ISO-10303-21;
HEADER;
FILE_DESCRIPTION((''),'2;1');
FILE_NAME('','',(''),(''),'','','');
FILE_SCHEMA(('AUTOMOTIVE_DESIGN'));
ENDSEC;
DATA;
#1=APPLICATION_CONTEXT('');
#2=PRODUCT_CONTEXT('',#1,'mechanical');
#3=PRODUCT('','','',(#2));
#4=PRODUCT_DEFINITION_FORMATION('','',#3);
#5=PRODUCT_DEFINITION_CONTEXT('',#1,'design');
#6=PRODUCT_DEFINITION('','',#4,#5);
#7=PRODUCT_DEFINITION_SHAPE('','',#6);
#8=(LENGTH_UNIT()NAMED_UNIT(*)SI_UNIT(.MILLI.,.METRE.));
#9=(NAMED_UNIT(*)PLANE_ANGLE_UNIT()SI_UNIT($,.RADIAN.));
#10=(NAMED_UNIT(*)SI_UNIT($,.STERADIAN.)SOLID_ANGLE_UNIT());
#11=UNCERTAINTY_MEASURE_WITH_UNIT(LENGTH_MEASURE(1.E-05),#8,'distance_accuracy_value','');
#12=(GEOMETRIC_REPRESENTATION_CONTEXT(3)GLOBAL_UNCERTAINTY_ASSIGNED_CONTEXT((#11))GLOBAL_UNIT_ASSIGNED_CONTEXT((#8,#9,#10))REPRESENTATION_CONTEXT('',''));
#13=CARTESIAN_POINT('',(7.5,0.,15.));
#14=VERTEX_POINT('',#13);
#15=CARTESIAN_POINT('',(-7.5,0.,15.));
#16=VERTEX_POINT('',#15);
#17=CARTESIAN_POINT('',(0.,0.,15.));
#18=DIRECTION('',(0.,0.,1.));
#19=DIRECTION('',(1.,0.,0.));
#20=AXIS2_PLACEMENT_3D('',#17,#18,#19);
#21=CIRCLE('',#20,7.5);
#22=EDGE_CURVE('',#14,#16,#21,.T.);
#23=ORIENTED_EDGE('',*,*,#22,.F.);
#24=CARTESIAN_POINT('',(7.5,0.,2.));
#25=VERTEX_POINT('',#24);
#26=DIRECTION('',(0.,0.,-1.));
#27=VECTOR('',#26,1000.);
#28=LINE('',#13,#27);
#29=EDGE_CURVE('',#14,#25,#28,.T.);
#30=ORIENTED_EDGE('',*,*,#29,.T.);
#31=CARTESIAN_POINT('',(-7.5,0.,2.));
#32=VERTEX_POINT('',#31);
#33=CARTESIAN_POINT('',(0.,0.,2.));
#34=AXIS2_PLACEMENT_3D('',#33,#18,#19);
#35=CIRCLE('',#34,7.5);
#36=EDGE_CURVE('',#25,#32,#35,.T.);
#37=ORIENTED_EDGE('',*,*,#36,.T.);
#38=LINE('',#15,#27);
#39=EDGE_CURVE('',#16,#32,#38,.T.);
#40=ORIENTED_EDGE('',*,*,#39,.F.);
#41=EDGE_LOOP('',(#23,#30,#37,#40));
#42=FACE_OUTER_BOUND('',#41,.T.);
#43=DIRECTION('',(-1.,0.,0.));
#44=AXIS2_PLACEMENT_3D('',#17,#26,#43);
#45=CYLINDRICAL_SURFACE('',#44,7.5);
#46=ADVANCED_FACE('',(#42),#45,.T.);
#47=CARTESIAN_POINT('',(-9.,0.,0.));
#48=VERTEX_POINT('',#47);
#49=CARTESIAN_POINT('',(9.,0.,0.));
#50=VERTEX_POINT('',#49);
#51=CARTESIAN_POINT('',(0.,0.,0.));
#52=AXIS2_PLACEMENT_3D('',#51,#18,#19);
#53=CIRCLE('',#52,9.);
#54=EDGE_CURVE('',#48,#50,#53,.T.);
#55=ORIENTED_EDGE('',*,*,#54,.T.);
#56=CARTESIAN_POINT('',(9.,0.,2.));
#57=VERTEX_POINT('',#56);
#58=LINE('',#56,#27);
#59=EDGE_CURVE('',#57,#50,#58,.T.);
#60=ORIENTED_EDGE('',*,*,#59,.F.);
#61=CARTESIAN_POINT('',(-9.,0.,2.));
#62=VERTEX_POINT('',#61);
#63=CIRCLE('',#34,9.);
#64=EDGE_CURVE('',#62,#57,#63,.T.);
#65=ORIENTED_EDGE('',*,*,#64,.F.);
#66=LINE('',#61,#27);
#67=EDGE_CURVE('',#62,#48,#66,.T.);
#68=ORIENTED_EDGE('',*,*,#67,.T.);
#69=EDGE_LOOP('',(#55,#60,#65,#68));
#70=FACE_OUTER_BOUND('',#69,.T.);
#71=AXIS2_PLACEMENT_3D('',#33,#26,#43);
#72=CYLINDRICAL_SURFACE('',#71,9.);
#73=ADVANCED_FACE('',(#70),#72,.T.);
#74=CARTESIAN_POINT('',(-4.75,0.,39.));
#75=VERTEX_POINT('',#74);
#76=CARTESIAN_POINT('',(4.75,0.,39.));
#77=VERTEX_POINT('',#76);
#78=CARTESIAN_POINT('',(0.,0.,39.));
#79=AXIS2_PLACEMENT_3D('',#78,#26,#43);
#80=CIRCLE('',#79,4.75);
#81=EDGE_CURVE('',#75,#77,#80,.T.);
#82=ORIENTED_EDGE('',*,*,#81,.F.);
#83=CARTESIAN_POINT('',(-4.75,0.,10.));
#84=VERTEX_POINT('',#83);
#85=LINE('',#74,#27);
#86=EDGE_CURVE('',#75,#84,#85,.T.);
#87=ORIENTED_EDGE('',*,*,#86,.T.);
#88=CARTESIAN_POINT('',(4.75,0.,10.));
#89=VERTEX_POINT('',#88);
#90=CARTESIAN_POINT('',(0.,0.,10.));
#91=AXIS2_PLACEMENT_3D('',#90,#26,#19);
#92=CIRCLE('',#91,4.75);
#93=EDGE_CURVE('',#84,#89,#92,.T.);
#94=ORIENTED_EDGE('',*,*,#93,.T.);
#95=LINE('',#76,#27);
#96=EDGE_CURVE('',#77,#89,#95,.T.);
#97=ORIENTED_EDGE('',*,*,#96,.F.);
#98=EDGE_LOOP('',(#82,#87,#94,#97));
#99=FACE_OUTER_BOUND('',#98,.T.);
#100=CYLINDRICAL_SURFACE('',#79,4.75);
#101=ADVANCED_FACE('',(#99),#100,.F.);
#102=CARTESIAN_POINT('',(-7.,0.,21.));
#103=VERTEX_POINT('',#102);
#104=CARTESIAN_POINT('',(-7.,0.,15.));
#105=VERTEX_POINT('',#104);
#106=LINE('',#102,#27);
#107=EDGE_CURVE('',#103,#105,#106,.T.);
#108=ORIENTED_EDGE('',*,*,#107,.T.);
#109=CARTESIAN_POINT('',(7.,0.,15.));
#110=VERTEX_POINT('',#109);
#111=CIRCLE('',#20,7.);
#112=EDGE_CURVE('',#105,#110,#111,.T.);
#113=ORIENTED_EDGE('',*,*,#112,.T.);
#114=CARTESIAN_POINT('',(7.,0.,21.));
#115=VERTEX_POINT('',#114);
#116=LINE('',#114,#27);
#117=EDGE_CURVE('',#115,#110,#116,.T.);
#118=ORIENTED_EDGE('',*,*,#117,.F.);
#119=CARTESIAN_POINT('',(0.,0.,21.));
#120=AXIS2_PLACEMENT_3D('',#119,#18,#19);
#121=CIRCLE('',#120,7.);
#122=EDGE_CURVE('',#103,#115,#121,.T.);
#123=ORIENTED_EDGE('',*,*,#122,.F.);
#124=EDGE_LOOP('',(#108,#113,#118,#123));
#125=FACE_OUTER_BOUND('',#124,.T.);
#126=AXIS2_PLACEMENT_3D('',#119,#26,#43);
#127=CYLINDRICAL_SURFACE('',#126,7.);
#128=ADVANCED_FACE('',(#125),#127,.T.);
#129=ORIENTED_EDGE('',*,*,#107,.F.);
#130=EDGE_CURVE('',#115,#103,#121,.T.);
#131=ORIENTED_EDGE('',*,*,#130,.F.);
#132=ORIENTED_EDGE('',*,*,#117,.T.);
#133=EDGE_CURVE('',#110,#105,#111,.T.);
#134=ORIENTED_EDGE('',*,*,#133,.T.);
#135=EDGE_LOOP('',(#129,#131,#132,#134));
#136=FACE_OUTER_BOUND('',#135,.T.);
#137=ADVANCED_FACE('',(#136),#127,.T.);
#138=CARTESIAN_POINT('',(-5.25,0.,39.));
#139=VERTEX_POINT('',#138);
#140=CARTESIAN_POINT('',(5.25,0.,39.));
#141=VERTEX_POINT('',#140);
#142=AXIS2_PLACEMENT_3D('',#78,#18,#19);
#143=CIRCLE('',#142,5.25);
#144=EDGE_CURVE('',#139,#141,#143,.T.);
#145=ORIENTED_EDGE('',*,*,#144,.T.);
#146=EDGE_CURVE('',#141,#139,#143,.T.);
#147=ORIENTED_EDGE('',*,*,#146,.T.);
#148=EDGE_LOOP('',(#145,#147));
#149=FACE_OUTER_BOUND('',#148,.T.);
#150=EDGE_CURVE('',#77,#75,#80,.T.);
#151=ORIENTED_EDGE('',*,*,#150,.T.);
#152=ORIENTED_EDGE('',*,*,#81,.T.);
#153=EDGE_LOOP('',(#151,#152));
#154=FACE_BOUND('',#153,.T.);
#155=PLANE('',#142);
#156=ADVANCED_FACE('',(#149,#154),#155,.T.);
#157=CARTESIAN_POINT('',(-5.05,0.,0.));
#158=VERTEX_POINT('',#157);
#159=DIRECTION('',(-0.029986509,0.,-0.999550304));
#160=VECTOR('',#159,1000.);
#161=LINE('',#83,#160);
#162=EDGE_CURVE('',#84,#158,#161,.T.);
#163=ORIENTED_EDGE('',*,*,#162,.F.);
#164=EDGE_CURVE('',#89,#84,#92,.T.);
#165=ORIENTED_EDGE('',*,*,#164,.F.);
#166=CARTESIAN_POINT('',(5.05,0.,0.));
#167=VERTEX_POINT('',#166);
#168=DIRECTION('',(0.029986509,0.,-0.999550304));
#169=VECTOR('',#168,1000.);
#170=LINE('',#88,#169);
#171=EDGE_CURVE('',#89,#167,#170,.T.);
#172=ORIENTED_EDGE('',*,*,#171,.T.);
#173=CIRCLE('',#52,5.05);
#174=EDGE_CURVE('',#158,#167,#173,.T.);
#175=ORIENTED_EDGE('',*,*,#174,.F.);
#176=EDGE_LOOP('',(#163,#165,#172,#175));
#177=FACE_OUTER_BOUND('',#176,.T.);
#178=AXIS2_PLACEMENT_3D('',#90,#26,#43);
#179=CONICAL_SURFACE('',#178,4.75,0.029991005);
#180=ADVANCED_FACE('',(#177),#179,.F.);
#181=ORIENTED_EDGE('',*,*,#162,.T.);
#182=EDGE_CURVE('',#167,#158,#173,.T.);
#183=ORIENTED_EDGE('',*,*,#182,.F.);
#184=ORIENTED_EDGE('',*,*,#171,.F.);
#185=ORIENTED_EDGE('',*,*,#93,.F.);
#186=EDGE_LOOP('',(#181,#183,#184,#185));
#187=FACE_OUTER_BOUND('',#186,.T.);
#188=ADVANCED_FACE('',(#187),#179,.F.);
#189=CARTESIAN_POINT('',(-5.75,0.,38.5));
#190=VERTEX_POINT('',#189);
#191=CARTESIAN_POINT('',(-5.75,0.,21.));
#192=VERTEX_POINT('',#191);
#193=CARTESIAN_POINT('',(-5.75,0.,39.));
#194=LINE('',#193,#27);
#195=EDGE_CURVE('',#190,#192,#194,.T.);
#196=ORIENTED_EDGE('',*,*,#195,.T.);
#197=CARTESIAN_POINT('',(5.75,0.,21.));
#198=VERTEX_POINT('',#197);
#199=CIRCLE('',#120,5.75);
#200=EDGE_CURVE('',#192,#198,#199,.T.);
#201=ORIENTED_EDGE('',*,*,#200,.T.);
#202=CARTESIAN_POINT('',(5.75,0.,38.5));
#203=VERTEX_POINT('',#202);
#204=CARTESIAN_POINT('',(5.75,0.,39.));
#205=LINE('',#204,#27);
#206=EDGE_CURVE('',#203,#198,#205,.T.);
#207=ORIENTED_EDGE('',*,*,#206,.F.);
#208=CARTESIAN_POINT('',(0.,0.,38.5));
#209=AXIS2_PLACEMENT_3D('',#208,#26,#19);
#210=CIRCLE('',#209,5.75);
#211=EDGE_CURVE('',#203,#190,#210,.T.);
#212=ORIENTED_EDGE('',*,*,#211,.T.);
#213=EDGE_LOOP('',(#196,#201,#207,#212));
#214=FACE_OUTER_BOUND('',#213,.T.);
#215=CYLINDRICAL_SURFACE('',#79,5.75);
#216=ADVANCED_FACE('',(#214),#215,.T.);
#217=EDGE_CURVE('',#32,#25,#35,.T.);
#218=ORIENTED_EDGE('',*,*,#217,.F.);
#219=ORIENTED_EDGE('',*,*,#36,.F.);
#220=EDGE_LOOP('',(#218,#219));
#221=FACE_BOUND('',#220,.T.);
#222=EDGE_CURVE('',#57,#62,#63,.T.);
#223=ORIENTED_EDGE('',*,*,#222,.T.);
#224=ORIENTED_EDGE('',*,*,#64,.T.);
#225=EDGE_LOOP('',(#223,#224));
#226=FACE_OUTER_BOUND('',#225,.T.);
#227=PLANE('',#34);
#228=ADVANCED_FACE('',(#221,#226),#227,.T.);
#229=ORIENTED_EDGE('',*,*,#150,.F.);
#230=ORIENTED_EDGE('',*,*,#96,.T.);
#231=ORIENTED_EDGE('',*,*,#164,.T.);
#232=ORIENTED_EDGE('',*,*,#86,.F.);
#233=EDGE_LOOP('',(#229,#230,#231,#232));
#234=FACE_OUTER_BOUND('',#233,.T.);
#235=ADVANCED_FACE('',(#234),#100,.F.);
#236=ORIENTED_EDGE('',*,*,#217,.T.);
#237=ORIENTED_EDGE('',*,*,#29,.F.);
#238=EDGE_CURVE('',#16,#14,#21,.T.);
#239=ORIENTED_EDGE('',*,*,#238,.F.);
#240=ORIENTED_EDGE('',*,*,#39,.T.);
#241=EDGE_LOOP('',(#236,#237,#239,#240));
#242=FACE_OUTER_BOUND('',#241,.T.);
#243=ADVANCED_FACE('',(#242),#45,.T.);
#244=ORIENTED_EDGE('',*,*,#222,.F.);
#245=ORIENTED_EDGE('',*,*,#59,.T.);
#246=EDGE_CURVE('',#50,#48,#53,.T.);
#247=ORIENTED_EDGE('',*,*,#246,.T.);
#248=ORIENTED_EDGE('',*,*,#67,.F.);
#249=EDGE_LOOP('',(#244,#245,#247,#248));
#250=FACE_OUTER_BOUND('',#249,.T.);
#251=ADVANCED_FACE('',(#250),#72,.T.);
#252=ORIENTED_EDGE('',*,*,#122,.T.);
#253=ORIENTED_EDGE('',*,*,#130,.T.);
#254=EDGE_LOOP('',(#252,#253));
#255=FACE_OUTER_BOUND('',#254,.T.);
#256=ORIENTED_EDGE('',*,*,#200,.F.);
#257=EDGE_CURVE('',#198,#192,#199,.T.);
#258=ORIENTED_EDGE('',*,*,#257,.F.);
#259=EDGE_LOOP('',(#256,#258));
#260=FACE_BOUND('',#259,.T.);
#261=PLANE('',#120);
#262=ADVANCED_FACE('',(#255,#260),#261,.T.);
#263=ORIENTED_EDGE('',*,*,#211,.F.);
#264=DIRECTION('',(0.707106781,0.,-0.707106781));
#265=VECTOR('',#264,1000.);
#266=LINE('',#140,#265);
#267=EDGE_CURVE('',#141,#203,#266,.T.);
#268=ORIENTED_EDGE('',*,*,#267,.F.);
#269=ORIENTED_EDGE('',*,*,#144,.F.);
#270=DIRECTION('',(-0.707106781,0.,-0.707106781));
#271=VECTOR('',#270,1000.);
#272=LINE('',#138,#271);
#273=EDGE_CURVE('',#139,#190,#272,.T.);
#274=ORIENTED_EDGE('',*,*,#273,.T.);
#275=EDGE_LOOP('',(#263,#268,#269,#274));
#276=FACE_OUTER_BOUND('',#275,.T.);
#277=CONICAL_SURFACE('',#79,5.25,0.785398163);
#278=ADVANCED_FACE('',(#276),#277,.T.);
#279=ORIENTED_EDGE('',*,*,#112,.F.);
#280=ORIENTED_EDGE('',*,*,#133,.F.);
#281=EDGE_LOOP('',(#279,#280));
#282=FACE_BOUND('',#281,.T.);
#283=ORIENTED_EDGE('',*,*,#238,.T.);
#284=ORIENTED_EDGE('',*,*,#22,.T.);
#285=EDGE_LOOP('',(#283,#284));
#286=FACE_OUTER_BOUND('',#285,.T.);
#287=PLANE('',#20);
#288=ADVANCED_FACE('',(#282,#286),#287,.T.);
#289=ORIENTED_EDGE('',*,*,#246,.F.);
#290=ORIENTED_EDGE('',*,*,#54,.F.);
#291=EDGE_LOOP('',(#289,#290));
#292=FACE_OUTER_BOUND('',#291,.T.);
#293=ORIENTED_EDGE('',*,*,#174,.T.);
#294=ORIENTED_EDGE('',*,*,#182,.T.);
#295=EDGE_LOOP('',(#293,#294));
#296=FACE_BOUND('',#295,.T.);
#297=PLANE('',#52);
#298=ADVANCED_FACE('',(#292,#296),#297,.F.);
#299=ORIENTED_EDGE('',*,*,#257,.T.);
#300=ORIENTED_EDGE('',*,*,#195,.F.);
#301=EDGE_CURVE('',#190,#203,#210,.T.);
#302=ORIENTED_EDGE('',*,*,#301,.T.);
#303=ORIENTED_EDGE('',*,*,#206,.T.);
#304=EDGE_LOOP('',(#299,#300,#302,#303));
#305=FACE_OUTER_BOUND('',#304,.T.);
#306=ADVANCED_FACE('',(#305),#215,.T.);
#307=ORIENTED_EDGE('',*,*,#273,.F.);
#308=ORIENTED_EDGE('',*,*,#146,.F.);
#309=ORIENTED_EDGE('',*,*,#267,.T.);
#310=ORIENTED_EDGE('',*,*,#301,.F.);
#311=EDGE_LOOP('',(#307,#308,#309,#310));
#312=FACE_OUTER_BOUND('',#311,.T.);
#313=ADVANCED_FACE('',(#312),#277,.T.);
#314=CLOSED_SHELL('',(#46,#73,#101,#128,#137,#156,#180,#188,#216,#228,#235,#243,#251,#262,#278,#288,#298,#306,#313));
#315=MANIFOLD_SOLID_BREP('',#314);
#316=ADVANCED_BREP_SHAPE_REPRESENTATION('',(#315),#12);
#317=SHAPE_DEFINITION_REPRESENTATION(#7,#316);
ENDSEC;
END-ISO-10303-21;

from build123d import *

# Parameters (mm, degrees)
SKETCH1_R           = 9
BOSS_EXTRUDE1_DEPTH = 2
SKETCH2_R           = 7.5
BOSS_EXTRUDE2_DEPTH = 13
SKETCH3_R           = 7
BOSS_EXTRUDE3_DEPTH = 6
SKETCH5_R           = 5.75
BOSS_EXTRUDE4_DEPTH = 18
SKETCH4_R           = 4.75
CUT_EXTRUDE1_DEPTH  = 42.024382994
CHAMFER1_SIZE       = 0.5
CHAMFER2_SIZE       = 0.3
CHAMFER2_SIZE2      = 10


with BuildPart() as part:
    # Sketch1 → Boss-Extrude1 (new body)
    with BuildSketch(Plane.XY):
        Circle(SKETCH1_R)
    extrude(amount=BOSS_EXTRUDE1_DEPTH)

    # Sketch2 → Boss-Extrude2 (add)
    with BuildSketch(Plane.XY.offset(2)):
        with Locations(Location((0, 0, 0), (0, 0, 180))):
            Circle(SKETCH2_R)
    extrude(amount=BOSS_EXTRUDE2_DEPTH)

    # Sketch3 → Boss-Extrude3 (add)
    with BuildSketch(Plane.XY.offset(15)):
        Circle(SKETCH3_R)
    extrude(amount=BOSS_EXTRUDE3_DEPTH)

    # Sketch5 → Boss-Extrude4 (add)
    with BuildSketch(Plane.XY.offset(21)):
        Circle(SKETCH5_R)
    extrude(amount=BOSS_EXTRUDE4_DEPTH)

    # Sketch4 → Cut-Extrude1 (cut, through all)
    with BuildSketch(Plane(origin=(0, 0, 0), x_dir=(-1, 0, 0), z_dir=(0, 0, -1))):
        Circle(SKETCH4_R)
    extrude(amount=-CUT_EXTRUDE1_DEPTH, mode=Mode.SUBTRACT)

    # Chamfer1
    chamfer1_edges = [part.edges().sort_by_distance(p)[0] for p in [
        (-5.75, 0, 39),
    ]]
    chamfer(chamfer1_edges, length=CHAMFER1_SIZE)

    # Chamfer2
    chamfer2_edges = [part.edges().sort_by_distance(p)[0] for p in [
        (4.75, 0, 0),
    ]]
    chamfer2_side = [part.faces().sort_by_distance(p)[0] for p in [
        (-8.745441559, 0, 0),
    ]]
    chamfer(chamfer2_edges, length=CHAMFER2_SIZE, length2=CHAMFER2_SIZE2, reference=chamfer2_side[0])


solid = part.part
